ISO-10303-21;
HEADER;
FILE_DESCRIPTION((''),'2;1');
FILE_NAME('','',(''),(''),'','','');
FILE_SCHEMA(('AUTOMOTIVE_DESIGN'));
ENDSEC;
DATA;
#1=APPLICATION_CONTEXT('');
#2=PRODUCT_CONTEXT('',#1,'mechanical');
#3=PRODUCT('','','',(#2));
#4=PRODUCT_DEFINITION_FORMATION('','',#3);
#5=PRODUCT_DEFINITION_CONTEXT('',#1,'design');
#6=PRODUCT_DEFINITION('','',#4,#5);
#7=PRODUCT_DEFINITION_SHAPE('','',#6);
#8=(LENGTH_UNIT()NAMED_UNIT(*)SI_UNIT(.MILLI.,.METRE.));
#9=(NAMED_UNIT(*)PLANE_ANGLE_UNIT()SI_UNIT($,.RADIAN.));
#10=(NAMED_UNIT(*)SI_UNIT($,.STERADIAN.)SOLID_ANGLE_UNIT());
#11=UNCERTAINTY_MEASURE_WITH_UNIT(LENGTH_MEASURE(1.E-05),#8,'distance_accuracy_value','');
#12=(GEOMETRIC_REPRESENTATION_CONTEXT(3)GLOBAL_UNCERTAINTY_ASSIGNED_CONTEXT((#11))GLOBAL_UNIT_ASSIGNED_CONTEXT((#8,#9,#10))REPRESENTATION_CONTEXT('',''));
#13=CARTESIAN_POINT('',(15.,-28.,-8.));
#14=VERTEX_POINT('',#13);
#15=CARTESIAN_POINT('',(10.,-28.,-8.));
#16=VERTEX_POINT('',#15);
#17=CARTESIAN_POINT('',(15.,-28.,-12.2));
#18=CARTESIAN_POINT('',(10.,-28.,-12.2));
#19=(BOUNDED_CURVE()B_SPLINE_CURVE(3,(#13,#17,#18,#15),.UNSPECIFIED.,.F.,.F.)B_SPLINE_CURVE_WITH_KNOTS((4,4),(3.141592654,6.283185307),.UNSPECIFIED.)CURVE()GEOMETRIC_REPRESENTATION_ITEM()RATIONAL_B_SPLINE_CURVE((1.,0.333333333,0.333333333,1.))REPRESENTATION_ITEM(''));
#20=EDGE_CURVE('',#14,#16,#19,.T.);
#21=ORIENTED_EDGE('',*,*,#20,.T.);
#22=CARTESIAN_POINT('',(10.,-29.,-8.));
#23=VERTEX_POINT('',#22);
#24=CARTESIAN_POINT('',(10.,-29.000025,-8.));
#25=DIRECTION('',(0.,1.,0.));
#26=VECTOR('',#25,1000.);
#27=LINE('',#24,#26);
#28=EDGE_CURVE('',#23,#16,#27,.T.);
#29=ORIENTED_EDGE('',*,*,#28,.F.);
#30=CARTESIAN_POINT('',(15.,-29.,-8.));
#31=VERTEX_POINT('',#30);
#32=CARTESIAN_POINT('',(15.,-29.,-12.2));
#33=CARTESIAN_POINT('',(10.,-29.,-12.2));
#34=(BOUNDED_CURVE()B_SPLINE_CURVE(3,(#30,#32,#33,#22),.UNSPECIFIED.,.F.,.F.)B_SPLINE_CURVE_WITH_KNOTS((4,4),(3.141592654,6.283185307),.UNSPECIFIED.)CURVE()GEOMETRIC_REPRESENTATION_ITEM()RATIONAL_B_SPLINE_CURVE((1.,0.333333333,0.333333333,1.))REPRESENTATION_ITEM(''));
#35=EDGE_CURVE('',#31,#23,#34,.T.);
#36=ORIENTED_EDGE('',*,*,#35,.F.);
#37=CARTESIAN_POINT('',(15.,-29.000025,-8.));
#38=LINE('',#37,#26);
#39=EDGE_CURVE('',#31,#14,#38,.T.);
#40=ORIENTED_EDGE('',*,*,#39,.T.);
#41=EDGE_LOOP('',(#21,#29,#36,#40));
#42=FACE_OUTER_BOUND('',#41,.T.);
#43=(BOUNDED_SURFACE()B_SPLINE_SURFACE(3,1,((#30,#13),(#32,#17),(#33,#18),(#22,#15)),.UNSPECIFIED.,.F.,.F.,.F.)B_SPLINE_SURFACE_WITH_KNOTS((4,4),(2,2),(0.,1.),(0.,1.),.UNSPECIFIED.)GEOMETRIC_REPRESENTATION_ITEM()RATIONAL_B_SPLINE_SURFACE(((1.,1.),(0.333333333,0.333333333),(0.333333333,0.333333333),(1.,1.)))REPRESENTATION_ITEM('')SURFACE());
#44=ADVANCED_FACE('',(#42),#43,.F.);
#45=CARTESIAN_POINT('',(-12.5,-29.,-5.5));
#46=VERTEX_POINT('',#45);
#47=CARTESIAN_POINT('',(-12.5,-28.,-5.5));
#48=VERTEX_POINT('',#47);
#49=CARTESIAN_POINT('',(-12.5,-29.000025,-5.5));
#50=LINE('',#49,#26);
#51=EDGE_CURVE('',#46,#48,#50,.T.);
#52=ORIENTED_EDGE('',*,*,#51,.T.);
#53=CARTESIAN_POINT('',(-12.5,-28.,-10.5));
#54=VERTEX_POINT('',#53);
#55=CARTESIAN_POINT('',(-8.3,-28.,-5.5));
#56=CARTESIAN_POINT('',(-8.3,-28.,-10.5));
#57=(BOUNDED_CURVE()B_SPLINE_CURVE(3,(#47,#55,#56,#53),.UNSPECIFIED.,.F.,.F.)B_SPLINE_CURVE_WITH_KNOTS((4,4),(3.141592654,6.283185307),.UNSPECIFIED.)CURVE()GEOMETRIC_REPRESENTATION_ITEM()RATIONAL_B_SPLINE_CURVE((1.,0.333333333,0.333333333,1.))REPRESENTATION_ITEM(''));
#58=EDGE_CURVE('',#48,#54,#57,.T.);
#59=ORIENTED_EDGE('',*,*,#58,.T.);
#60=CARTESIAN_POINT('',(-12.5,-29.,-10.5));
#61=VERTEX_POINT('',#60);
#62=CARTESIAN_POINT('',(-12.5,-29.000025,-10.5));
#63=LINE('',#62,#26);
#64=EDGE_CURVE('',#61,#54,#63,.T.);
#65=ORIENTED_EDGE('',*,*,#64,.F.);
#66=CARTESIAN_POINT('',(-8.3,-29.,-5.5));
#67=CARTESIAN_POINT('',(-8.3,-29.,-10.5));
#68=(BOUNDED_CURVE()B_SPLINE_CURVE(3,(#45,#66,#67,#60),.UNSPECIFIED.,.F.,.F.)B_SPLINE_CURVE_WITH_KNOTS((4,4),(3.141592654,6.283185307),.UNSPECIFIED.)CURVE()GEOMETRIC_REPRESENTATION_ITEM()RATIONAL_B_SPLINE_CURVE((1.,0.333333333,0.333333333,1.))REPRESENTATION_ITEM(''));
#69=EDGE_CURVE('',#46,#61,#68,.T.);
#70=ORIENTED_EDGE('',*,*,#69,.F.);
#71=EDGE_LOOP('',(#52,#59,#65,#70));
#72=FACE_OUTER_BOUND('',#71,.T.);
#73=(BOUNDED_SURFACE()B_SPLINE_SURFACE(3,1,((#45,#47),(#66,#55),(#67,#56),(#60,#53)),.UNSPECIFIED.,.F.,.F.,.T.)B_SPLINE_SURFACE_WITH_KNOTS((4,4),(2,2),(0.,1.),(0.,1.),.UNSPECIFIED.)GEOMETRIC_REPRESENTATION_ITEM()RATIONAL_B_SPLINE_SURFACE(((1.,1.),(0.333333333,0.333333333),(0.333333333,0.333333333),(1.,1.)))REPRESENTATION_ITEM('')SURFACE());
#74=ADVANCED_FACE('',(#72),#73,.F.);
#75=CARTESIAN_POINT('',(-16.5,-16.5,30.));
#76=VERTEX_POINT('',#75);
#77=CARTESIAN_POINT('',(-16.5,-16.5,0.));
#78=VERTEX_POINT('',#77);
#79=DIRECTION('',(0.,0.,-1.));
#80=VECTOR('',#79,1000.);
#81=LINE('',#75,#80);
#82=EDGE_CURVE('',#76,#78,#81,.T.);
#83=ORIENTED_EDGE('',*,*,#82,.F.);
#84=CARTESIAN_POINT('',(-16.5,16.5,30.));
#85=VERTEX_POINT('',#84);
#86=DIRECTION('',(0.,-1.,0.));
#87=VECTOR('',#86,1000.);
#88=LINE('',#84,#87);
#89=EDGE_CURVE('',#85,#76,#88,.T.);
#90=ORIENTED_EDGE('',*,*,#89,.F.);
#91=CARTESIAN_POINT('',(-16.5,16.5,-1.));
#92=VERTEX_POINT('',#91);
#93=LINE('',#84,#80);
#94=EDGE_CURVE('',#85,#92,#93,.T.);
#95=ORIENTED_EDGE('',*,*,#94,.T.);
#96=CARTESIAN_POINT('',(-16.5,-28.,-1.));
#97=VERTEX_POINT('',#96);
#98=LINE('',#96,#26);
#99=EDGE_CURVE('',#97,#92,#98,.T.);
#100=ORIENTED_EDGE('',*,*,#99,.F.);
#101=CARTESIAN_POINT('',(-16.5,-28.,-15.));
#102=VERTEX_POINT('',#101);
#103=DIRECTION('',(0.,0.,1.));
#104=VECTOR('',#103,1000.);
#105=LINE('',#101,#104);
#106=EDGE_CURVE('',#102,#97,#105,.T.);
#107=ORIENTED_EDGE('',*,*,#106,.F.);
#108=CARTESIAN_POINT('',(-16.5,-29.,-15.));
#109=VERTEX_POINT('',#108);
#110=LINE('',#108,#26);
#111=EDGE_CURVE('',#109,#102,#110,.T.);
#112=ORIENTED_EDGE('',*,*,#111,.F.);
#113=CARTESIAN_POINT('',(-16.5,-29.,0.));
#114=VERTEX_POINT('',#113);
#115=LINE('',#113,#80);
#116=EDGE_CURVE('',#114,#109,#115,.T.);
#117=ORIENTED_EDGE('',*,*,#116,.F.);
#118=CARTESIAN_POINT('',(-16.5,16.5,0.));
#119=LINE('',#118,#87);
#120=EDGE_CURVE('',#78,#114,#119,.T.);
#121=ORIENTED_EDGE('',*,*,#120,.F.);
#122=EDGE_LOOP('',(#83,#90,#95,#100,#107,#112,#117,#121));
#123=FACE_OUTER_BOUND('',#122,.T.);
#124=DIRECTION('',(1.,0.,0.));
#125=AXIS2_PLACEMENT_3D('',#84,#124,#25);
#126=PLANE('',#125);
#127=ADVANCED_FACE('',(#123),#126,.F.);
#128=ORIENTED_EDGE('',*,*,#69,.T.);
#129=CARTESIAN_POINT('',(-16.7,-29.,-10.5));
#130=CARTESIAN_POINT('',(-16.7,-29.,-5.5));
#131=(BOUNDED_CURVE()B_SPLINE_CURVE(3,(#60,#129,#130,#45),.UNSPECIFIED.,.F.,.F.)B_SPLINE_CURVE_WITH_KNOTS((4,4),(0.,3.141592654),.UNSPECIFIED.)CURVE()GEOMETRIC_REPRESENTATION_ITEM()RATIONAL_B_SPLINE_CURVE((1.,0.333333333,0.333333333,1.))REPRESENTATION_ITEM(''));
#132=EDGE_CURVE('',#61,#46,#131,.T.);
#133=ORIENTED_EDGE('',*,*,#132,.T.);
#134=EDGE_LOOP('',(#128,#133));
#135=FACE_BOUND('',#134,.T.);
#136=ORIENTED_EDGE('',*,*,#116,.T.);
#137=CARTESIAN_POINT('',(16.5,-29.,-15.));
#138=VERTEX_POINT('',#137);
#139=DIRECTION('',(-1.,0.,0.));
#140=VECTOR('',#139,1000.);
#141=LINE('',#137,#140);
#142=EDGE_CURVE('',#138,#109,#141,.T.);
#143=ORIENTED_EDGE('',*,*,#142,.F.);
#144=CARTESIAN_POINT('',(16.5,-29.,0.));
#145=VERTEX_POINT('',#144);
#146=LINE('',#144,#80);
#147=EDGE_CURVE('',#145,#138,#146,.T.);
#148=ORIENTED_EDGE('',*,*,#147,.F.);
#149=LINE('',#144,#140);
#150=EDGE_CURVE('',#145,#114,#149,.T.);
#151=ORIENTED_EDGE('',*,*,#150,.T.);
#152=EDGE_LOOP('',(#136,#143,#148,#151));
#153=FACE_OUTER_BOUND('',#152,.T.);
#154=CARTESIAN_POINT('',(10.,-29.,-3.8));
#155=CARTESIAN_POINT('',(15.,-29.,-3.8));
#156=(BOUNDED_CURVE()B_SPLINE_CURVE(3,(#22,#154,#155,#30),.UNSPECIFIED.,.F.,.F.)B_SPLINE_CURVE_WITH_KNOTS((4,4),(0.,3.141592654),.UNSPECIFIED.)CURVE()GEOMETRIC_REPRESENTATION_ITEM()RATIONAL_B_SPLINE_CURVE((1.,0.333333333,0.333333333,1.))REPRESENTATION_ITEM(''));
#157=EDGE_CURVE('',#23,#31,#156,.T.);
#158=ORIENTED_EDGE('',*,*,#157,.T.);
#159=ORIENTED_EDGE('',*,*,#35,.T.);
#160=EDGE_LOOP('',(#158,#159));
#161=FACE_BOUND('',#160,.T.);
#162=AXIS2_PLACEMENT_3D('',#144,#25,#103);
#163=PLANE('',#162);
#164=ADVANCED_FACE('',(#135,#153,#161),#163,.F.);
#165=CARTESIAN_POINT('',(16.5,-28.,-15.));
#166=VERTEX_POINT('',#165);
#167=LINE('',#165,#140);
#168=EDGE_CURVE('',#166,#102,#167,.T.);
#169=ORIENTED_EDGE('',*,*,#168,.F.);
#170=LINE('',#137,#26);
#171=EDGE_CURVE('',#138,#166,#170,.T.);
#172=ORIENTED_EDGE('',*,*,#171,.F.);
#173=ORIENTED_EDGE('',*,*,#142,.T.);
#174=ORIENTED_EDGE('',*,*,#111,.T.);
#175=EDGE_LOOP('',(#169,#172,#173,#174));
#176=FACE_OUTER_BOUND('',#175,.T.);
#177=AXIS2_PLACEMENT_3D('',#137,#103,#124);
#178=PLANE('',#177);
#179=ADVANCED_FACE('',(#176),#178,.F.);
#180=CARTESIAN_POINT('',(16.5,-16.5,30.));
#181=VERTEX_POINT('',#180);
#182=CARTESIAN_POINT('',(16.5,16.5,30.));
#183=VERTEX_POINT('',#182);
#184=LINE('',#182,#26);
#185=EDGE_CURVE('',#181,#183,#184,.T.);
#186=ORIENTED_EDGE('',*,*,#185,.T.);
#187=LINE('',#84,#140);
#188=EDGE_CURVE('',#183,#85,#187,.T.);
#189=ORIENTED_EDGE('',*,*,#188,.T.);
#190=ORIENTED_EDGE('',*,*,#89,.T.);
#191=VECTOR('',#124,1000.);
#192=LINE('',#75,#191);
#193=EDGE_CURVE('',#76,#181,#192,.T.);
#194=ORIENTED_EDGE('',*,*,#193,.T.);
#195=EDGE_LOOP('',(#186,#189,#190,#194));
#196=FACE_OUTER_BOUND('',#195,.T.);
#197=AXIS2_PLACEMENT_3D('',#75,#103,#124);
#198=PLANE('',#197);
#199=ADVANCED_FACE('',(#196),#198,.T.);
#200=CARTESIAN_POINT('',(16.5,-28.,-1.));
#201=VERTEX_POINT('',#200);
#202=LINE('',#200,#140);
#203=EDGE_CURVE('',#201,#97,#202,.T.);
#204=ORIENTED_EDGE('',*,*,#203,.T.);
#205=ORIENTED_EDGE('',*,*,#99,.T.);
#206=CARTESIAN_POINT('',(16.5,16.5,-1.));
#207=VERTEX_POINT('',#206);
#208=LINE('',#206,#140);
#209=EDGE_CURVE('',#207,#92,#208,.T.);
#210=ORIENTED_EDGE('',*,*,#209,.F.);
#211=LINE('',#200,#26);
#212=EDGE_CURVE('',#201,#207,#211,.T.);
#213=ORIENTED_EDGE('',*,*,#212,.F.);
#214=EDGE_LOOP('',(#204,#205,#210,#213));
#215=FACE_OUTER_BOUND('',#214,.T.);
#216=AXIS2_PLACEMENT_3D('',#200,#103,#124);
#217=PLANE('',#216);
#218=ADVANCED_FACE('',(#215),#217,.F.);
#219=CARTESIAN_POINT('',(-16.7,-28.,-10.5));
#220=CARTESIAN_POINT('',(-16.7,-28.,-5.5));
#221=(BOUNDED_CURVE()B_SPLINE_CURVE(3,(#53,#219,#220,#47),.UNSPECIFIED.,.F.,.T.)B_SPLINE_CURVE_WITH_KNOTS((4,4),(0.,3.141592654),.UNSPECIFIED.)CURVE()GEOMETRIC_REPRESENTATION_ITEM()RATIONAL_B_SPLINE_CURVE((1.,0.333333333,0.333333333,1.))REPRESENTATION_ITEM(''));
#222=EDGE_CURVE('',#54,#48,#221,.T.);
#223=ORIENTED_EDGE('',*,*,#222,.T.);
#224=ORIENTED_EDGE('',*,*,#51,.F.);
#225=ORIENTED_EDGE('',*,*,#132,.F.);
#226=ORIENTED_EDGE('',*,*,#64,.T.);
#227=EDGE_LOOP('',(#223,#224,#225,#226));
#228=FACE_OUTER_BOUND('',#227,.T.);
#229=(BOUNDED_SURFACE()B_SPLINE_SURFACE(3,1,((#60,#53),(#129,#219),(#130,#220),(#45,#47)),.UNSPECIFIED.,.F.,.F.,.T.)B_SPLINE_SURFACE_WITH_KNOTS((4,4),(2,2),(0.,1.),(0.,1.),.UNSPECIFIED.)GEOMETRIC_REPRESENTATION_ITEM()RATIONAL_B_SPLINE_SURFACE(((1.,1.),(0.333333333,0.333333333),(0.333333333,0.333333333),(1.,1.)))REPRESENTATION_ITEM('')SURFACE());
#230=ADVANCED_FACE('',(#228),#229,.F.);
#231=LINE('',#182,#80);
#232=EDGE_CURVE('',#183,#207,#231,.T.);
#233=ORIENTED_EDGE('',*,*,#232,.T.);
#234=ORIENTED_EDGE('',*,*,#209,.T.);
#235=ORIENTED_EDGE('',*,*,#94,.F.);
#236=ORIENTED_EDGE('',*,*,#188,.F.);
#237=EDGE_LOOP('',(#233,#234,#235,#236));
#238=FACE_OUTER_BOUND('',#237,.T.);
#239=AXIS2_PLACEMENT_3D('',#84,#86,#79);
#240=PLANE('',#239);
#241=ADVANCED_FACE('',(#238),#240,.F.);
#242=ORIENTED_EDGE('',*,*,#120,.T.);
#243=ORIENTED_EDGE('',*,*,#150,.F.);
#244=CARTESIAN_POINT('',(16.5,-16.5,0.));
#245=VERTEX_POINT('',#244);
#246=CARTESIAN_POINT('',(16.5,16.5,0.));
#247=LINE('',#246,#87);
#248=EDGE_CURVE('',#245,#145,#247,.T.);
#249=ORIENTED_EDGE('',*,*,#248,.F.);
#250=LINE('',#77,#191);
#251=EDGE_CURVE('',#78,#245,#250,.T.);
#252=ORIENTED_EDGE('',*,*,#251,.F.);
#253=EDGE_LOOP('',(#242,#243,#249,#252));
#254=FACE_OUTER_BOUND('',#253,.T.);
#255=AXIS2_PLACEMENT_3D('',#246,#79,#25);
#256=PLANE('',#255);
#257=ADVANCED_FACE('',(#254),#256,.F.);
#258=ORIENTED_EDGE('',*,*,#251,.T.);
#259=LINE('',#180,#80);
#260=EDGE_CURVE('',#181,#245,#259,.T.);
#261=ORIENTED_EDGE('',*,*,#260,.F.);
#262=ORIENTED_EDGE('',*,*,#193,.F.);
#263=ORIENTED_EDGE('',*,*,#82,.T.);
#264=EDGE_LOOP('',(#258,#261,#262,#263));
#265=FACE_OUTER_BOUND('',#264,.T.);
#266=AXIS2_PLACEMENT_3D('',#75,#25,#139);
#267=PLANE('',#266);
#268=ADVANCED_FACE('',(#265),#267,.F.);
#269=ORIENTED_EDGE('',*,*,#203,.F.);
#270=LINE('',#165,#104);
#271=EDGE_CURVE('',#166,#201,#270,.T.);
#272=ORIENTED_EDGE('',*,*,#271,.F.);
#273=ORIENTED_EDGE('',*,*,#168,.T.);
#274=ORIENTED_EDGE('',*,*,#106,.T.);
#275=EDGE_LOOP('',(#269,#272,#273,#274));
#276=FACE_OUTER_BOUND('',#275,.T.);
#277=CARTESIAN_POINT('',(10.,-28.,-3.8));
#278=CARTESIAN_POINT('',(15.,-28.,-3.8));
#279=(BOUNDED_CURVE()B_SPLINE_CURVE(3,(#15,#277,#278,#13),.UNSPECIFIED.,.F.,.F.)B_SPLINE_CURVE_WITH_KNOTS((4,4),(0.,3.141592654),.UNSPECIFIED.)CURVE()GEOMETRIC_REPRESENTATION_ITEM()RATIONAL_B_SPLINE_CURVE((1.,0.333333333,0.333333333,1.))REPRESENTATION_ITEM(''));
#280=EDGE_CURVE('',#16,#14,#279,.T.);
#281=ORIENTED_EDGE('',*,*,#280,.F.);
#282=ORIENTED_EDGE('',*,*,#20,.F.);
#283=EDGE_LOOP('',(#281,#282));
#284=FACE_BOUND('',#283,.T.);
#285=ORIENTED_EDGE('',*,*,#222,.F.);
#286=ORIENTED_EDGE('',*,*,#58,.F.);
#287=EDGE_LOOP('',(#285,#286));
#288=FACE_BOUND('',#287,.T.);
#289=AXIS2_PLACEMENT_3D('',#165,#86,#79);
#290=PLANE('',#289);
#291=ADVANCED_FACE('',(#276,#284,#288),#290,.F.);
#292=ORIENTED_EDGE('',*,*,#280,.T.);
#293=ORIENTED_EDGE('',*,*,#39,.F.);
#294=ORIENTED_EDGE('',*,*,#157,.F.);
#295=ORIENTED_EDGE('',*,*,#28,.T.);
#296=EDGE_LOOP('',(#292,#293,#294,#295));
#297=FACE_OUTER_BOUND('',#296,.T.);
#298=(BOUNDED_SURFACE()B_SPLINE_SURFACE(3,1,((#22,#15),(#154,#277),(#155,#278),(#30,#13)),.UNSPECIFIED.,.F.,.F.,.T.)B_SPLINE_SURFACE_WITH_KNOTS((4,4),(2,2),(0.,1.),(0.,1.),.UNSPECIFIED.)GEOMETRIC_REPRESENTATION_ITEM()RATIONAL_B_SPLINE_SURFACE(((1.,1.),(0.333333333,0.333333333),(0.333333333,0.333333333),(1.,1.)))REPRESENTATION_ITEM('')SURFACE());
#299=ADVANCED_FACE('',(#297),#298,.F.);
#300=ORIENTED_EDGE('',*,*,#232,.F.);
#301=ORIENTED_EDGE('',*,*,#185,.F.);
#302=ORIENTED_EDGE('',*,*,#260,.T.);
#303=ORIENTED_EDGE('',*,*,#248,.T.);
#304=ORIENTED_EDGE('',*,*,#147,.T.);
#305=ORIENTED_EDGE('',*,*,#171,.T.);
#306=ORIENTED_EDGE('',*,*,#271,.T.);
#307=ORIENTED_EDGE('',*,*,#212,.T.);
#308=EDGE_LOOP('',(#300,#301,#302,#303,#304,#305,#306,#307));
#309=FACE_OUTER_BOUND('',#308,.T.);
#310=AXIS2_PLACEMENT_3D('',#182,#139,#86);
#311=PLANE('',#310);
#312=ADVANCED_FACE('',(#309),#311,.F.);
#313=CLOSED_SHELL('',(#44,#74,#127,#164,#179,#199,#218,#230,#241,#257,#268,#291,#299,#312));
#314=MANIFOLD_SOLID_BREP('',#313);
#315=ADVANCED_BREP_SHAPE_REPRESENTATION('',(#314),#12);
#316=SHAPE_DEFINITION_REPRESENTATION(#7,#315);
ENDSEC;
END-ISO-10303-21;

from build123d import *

# Parameters (mm, degrees)
SKETCH1_W          = 33
SKETCH1_H          = 33
EXTRUDE1_DEPTH     = 30
EXTRUDE2_DEPTH     = 16.5
SKETCH4_RX         = 2.5
SKETCH4_RY         = 2.1
CUT_EXTRUDE1_DEPTH = 57.147128155


with BuildPart() as part:
    # Sketch1 → Extrude1 (new body)
    with BuildSketch(Plane.XY):
        Rectangle(SKETCH1_W, SKETCH1_H)
    extrude(amount=EXTRUDE1_DEPTH)

    # Sketch3 → Extrude2 (add, symmetric)
    with BuildSketch(Plane(origin=(0, 0, 0), x_dir=(0, 0, -1), z_dir=(1, 0, 0))):
        Polygon((0, 16.5), (0, -29), (15, -29), (15, -28), (1, -28), (1, 16.5), align=None)
    extrude(amount=EXTRUDE2_DEPTH, both=True)

    # Sketch4 → Cut-Extrude1 (cut, through all)
    with BuildSketch(Plane(origin=(0, -28, 0), x_dir=(1, 0, 0), z_dir=(0, 1, 0))):
        with Locations(Location((-12.5, 8), (0, 0, 90))):
            Ellipse(SKETCH4_RX, SKETCH4_RY)
        with Locations(Location((12.5, 8), (0, 0, -180))):
            Ellipse(SKETCH4_RX, SKETCH4_RY)
    extrude(amount=-CUT_EXTRUDE1_DEPTH, mode=Mode.SUBTRACT)


solid = part.part
